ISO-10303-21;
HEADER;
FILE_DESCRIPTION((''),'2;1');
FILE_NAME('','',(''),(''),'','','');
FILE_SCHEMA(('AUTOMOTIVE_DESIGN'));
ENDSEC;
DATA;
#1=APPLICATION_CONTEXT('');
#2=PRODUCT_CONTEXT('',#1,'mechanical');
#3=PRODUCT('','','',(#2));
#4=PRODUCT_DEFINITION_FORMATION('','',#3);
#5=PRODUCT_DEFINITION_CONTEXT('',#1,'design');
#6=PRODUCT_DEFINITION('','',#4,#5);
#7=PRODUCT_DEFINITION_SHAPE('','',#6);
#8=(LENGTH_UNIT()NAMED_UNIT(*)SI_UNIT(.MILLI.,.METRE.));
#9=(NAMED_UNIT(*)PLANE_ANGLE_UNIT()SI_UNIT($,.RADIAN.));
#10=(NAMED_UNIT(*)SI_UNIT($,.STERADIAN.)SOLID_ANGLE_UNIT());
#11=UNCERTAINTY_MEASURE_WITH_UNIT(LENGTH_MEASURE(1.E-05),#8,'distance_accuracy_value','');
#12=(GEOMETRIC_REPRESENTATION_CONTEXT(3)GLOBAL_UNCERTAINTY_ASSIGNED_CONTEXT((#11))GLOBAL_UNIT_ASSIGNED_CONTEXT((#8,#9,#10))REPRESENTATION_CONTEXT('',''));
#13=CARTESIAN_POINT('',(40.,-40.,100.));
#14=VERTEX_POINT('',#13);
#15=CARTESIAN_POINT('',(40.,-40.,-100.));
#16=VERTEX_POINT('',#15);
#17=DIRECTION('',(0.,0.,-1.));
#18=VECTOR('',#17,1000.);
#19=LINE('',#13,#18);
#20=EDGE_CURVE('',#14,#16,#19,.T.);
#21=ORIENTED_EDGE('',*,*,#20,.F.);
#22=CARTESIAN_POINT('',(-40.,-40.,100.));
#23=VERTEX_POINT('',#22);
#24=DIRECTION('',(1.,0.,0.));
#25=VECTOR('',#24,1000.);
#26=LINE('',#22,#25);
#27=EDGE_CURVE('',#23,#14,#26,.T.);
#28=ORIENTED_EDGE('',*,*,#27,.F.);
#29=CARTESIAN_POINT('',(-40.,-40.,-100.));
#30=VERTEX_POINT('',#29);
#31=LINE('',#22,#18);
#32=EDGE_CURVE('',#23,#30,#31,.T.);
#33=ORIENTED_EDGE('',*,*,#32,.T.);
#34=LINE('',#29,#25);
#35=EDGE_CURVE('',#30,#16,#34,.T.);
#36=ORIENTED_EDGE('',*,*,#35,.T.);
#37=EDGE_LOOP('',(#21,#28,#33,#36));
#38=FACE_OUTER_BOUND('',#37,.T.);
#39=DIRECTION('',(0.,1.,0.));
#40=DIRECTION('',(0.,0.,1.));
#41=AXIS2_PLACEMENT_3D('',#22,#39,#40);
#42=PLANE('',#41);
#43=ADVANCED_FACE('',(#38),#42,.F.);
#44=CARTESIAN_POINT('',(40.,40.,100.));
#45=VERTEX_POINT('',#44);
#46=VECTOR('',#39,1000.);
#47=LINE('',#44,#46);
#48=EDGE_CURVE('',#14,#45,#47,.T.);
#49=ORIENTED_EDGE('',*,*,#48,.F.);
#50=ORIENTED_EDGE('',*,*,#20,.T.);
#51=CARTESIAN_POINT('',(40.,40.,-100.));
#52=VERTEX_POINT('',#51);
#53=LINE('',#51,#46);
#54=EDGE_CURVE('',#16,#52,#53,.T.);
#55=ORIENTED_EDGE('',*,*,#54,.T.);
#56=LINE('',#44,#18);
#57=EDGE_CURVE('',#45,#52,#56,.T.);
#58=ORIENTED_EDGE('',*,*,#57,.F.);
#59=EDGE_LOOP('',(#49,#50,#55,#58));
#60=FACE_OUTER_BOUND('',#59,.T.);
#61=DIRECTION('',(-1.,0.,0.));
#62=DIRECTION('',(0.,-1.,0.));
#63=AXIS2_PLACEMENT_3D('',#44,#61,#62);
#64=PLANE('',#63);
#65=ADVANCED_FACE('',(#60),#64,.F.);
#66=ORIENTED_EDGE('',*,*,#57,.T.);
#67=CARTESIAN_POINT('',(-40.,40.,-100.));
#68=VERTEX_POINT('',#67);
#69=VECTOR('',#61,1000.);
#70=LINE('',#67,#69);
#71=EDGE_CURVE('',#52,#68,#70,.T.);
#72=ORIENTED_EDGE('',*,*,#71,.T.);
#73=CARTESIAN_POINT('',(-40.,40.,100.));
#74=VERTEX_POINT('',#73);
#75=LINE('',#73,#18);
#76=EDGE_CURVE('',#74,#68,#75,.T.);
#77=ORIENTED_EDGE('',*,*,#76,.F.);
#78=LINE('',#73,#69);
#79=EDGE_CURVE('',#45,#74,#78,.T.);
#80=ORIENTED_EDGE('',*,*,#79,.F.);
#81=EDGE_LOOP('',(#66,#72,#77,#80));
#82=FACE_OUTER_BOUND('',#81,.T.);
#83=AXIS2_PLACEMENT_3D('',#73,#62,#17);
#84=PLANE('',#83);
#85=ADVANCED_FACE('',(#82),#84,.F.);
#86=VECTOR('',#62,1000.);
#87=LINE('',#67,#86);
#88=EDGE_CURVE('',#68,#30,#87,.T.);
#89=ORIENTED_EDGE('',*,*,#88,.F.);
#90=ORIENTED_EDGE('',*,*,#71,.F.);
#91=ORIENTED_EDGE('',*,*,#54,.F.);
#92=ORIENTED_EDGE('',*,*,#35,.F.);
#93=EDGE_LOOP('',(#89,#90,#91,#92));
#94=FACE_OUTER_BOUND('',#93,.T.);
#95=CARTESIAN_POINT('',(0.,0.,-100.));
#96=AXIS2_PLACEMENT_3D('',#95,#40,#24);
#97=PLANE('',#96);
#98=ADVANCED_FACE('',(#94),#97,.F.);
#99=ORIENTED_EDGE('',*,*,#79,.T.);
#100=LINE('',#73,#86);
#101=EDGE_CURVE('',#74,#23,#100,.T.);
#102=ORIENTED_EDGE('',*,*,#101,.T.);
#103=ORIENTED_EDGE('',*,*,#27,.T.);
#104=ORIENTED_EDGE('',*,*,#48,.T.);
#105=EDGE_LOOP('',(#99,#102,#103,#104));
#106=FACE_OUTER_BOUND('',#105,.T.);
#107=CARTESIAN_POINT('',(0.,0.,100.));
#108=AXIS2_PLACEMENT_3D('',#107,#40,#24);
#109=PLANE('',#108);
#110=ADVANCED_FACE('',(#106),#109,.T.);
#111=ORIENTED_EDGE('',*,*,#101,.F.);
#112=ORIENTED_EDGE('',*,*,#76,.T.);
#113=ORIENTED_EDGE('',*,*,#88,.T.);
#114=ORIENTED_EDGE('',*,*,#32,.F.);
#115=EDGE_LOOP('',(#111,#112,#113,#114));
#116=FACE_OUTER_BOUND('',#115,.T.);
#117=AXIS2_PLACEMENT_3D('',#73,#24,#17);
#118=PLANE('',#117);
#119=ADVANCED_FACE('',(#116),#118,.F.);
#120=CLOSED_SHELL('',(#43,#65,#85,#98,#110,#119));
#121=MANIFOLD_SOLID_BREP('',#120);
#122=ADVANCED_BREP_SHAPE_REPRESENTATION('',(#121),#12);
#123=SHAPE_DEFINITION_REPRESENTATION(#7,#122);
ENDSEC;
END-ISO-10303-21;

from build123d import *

# Parameters (mm, degrees)
SKETCH1_W           = 80
SKETCH1_H           = 80
BOSS_EXTRUDE1_DEPTH = 100


with BuildPart() as part:
    # Sketch1 → Boss-Extrude1 (new, symmetric)
    with BuildSketch(Plane.XY):
        Rectangle(SKETCH1_W, SKETCH1_H)
    extrude(amount=BOSS_EXTRUDE1_DEPTH, both=True)


solid = part.part
